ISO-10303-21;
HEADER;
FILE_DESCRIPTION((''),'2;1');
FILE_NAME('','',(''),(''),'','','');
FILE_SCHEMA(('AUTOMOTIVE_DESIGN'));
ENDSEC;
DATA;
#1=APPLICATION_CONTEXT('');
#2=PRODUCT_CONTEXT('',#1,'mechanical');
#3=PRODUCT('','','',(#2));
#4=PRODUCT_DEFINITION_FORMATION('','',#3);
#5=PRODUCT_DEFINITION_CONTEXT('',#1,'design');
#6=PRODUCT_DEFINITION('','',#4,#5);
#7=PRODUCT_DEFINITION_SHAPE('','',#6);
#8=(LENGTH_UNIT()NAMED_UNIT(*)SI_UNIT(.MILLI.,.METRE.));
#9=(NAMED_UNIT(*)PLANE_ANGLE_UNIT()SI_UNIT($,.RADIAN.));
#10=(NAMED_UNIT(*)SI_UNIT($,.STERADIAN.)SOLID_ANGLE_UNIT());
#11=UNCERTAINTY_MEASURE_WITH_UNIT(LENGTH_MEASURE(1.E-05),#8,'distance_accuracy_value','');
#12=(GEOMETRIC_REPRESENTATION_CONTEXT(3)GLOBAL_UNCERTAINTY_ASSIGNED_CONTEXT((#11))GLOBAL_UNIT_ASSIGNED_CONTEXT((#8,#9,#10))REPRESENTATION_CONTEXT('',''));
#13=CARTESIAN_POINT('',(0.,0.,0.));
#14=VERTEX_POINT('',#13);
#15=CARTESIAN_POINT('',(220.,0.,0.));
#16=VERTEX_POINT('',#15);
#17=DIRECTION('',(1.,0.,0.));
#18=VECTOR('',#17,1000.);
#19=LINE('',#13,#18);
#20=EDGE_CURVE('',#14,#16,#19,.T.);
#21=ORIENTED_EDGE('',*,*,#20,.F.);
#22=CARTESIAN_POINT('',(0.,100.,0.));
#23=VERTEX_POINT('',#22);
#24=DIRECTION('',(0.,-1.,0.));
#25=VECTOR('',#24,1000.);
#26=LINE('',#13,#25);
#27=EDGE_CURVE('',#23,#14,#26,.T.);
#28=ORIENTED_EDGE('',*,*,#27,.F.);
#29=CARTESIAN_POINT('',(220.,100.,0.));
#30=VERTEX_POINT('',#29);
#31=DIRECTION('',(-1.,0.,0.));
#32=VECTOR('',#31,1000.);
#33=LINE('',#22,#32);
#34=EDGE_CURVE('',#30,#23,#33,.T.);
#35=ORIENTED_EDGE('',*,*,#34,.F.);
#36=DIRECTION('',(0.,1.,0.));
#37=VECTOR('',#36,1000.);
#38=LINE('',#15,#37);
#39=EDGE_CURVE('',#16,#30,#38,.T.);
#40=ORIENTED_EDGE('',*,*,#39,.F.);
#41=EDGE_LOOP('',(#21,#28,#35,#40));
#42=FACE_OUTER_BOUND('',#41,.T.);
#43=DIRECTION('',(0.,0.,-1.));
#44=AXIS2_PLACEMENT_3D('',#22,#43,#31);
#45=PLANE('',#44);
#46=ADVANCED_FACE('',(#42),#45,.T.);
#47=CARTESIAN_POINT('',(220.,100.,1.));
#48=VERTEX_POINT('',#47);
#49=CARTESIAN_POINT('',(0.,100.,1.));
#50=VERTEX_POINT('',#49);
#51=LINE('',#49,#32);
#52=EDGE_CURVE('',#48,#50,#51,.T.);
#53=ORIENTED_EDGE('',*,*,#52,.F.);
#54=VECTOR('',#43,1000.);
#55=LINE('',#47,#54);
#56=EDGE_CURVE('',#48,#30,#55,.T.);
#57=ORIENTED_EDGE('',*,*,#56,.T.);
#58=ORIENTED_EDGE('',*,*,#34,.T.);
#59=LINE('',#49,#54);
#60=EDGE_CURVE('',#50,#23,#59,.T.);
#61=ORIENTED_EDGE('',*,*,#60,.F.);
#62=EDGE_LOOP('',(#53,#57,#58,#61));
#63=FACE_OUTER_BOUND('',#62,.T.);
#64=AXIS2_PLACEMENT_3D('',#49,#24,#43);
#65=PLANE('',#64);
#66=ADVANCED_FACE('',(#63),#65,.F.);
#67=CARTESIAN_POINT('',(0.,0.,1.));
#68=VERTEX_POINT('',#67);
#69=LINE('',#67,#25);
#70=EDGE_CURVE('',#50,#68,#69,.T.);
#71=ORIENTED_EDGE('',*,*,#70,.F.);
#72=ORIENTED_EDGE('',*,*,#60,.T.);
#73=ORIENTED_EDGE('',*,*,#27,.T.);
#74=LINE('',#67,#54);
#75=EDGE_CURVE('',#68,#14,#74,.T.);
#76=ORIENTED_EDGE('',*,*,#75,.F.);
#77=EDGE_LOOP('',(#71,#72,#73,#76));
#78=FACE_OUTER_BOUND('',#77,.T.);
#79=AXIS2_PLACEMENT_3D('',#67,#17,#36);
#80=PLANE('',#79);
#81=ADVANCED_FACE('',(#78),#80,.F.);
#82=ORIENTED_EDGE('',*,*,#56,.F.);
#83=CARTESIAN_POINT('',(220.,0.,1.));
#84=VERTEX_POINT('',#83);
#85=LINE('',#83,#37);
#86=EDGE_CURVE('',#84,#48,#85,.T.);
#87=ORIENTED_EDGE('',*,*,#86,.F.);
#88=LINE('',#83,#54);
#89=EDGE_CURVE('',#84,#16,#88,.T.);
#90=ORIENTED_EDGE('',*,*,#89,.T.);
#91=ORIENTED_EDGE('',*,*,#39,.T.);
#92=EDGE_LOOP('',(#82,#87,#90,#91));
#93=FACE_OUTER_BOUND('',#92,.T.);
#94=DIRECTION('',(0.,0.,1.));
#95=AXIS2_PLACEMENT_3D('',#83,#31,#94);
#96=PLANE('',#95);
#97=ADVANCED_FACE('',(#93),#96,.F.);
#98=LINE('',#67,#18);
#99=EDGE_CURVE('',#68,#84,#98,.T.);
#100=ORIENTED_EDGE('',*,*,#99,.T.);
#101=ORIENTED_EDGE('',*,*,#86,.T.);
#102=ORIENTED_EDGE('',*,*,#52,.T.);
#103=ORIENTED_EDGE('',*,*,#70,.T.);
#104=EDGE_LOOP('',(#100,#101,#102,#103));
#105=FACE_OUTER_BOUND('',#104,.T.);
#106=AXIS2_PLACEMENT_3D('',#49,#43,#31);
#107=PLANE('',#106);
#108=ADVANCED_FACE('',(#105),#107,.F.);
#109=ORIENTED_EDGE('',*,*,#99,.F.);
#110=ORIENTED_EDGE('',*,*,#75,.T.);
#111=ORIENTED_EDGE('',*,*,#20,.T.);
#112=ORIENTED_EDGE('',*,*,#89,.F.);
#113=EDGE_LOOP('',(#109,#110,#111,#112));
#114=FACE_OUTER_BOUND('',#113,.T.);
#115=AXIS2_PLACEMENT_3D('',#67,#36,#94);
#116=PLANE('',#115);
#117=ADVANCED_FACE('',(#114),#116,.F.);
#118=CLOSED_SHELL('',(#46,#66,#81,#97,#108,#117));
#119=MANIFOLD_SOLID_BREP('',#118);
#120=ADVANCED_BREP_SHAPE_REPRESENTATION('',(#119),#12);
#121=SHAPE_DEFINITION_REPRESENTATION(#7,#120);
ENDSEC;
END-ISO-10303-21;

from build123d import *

# Parameters (mm, degrees)
SKETCH_1_W      = 220
SKETCH_1_H      = 100
EXTRUDE_1_DEPTH = 1


with BuildPart() as part:
    # 草图1 → 凸台-拉伸1 (new body)
    with BuildSketch(Plane.XY):
        with Locations((110, 50)):
            Rectangle(SKETCH_1_W, SKETCH_1_H)
    extrude(amount=EXTRUDE_1_DEPTH)


solid = part.part
